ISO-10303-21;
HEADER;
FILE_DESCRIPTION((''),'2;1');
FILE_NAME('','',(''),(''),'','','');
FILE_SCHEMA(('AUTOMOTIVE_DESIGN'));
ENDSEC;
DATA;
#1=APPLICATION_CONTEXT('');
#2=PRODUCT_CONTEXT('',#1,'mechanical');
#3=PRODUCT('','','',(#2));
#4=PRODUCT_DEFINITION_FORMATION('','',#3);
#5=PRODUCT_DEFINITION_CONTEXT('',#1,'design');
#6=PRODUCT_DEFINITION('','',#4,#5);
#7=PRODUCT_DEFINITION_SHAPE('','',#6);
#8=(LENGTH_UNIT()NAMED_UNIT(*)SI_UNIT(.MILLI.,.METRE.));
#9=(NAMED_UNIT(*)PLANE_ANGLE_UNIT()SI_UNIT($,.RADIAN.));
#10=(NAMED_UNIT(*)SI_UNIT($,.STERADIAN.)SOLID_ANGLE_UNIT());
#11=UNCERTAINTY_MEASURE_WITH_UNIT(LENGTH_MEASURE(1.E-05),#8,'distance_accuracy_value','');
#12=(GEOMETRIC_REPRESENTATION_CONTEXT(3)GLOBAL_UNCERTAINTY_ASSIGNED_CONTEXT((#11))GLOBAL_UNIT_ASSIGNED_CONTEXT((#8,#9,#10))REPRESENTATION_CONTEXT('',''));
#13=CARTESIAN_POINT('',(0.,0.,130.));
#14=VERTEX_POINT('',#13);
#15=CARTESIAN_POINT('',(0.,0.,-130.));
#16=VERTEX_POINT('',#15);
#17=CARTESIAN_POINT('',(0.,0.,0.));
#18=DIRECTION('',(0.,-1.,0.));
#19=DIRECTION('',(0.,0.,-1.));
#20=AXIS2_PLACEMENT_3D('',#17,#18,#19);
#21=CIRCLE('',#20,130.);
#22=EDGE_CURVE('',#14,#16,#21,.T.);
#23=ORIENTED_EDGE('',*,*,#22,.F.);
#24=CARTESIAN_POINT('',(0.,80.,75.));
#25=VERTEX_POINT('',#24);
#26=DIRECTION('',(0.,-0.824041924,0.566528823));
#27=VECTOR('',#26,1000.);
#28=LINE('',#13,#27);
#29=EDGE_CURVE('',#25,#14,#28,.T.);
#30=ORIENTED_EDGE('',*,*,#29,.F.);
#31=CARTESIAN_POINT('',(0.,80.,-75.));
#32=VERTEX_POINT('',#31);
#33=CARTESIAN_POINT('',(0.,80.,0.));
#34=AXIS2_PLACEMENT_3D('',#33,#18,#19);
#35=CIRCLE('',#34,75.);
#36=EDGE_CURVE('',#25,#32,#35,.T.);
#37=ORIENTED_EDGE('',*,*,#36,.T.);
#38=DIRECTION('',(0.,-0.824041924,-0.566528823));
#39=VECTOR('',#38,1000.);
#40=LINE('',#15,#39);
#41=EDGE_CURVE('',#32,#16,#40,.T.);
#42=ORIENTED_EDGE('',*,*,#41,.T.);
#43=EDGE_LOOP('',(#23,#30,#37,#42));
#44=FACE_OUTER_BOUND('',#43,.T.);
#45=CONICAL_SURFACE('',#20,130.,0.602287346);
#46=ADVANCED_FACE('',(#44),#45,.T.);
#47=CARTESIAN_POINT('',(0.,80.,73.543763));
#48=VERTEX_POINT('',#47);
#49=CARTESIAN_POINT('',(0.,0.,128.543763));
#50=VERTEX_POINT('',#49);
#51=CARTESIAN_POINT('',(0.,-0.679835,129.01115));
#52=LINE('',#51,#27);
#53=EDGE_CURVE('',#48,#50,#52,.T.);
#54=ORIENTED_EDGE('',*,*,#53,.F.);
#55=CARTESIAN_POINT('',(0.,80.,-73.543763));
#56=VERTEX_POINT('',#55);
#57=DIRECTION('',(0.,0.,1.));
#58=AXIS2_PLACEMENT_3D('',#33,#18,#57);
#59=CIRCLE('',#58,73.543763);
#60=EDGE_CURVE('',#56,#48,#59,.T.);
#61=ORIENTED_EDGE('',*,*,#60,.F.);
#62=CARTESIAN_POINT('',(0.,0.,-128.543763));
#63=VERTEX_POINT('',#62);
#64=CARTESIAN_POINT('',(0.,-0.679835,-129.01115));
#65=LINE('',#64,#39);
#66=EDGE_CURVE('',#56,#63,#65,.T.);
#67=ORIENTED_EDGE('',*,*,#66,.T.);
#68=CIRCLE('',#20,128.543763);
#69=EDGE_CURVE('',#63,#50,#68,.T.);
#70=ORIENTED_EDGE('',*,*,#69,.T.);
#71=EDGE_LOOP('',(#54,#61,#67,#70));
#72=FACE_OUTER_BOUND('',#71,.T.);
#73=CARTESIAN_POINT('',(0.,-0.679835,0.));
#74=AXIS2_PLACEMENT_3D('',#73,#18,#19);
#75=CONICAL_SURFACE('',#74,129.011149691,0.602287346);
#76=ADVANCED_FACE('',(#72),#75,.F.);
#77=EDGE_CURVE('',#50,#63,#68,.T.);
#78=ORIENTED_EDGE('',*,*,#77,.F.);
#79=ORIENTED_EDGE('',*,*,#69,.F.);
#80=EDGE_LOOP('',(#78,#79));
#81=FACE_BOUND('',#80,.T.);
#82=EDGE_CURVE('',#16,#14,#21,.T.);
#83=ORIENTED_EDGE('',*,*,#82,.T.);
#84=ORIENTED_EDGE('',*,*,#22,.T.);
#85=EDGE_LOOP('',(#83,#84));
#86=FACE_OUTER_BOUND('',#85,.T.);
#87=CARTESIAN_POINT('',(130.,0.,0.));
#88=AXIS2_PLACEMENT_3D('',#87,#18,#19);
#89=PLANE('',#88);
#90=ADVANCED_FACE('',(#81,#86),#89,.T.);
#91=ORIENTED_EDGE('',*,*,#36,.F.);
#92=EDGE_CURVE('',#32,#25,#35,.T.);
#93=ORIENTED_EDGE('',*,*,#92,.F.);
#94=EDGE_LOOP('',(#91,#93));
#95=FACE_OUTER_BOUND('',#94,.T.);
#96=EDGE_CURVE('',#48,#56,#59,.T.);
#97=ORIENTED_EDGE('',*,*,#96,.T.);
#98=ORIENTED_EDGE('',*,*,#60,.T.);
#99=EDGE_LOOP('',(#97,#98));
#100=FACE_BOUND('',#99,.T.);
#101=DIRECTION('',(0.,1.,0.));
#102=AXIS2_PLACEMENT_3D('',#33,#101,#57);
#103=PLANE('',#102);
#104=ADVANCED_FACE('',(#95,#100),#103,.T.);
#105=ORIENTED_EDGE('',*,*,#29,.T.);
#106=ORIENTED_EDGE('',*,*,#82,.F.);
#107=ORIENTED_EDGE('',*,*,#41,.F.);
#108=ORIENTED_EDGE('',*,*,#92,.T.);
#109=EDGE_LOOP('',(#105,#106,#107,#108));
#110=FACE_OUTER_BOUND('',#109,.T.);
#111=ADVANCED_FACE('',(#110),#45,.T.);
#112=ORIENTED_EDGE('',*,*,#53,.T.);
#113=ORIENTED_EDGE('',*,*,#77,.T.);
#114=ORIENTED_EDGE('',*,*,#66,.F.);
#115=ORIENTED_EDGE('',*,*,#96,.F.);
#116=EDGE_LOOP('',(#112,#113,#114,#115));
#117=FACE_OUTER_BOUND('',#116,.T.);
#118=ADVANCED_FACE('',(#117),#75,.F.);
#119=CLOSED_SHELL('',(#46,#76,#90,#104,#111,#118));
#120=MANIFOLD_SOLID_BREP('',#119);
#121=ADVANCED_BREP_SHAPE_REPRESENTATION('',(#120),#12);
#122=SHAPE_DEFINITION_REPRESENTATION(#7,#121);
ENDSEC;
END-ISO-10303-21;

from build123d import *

# Parameters (mm, degrees)
SHELL1_T = -1.2


with BuildPart() as part:
    # Sketch3 → Revolve1 (revolve)
    with BuildSketch(Plane.XY, mode=Mode.PRIVATE) as revolve1_sk:
        Polygon((0, 80), (75, 80), (130, 0), (0, 0), align=None)
    revolve(revolve1_sk.sketch.rotate(Axis((0, 0, 0), (0, 1, 0)), 90), axis=Axis((0, 0, 0), (0, 1, 0)))

    # Shell1
    shell1_openings = [part.faces().sort_by_distance(p)[0] for p in [
        (0, 0, 0),
        (0, 80, 0),
    ]]
    offset(amount=SHELL1_T, openings=shell1_openings, kind=Kind.INTERSECTION)


solid = part.part
